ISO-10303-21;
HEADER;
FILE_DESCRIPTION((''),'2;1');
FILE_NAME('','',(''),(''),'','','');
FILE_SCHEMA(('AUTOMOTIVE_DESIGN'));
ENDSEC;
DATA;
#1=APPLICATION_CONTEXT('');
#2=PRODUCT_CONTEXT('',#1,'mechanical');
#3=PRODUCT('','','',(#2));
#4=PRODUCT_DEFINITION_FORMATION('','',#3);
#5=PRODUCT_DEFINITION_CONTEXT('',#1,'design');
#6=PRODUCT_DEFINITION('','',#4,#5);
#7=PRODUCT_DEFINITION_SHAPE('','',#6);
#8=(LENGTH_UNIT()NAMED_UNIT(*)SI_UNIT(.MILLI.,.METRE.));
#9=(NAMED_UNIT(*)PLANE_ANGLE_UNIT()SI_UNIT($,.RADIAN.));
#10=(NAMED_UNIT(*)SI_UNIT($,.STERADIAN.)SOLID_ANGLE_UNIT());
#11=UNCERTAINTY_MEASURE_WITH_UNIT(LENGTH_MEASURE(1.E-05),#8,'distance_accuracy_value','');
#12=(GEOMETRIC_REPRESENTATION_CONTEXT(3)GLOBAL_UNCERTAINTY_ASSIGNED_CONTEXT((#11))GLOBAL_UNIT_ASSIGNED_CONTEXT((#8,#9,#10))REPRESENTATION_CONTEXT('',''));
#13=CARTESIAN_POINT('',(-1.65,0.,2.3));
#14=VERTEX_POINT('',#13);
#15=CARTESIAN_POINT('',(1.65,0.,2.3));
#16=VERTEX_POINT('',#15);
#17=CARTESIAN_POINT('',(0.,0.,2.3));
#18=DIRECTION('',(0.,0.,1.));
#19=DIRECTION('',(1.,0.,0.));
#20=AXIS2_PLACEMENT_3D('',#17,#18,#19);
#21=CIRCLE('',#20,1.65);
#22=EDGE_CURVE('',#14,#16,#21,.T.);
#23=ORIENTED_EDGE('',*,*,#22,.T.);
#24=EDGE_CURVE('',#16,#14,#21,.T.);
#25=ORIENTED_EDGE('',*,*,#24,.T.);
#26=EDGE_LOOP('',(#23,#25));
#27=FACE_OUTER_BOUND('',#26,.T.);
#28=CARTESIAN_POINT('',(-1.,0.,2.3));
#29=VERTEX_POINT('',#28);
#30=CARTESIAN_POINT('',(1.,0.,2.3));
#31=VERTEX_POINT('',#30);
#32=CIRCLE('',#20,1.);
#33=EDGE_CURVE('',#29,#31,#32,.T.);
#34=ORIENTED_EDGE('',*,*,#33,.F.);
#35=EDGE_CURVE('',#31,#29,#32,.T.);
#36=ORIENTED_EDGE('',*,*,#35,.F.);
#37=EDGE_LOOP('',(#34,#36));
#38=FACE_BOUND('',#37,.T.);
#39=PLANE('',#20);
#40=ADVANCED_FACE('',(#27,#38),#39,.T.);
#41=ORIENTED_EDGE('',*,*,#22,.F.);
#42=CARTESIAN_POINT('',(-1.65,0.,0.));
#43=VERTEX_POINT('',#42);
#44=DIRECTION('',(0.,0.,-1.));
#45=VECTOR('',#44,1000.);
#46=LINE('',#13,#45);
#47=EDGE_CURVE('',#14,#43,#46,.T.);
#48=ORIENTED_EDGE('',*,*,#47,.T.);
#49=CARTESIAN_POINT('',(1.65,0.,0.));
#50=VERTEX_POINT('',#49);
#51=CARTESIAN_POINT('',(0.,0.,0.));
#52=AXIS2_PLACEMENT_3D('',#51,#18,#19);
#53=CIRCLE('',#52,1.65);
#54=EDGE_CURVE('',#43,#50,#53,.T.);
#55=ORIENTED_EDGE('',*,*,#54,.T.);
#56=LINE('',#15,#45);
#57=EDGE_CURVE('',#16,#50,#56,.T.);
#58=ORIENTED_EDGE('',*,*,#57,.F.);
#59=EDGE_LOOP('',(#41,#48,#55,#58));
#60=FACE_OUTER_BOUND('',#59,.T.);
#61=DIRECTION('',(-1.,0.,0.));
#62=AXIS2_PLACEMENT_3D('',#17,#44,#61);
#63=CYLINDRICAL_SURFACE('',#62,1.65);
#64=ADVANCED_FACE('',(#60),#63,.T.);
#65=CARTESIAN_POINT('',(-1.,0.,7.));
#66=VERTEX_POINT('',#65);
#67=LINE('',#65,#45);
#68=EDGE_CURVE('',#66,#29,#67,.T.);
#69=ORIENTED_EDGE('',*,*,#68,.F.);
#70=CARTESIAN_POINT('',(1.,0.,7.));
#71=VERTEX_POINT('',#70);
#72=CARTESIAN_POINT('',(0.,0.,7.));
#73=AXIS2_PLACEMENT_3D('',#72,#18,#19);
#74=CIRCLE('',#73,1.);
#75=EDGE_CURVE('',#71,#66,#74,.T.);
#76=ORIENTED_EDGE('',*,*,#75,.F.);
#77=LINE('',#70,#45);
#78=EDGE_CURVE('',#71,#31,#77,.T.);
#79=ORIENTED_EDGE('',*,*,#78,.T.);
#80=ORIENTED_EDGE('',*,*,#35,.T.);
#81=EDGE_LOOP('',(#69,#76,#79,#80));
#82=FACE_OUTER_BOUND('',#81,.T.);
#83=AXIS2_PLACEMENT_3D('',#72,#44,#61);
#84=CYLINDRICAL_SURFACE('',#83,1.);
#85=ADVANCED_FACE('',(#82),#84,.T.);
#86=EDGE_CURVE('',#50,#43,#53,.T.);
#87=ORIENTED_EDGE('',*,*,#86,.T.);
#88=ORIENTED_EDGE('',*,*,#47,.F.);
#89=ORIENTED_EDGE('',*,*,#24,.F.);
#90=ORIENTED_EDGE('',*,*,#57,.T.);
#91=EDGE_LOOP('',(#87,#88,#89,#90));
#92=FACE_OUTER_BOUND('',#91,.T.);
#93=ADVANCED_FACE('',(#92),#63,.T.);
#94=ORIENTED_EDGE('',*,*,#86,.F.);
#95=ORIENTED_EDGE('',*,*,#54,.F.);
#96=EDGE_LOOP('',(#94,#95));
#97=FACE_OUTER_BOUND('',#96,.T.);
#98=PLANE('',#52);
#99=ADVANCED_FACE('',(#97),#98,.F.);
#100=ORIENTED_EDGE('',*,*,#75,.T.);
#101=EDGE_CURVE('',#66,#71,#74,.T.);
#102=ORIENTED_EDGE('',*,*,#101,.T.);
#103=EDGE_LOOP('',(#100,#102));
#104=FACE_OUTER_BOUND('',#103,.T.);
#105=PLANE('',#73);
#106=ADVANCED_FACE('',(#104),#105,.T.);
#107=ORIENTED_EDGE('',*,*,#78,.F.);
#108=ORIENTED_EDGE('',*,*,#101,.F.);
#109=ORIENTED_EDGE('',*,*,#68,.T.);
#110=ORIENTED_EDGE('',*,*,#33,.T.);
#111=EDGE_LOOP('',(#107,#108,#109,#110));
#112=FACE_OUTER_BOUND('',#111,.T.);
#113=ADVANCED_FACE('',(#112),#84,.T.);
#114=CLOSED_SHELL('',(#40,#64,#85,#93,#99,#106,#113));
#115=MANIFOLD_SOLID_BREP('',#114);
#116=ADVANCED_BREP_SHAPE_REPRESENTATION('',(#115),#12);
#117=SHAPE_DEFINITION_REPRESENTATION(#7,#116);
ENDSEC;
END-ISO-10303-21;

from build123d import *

# Parameters (mm, degrees)
SKETCH_1_R      = 1.65
EXTRUDE_1_DEPTH = 2.3
SKETCH_2_R      = 1
EXTRUDE_2_DEPTH = 4.7


with BuildPart() as part:
    # 草图1 → 凸台-拉伸1 (new body)
    with BuildSketch(Plane.XY):
        Circle(SKETCH_1_R)
    extrude(amount=EXTRUDE_1_DEPTH)

    # 草图2 → 凸台-拉伸2 (add)
    with BuildSketch(Plane.XY.offset(2.3)):
        Circle(SKETCH_2_R)
    extrude(amount=EXTRUDE_2_DEPTH)


solid = part.part
